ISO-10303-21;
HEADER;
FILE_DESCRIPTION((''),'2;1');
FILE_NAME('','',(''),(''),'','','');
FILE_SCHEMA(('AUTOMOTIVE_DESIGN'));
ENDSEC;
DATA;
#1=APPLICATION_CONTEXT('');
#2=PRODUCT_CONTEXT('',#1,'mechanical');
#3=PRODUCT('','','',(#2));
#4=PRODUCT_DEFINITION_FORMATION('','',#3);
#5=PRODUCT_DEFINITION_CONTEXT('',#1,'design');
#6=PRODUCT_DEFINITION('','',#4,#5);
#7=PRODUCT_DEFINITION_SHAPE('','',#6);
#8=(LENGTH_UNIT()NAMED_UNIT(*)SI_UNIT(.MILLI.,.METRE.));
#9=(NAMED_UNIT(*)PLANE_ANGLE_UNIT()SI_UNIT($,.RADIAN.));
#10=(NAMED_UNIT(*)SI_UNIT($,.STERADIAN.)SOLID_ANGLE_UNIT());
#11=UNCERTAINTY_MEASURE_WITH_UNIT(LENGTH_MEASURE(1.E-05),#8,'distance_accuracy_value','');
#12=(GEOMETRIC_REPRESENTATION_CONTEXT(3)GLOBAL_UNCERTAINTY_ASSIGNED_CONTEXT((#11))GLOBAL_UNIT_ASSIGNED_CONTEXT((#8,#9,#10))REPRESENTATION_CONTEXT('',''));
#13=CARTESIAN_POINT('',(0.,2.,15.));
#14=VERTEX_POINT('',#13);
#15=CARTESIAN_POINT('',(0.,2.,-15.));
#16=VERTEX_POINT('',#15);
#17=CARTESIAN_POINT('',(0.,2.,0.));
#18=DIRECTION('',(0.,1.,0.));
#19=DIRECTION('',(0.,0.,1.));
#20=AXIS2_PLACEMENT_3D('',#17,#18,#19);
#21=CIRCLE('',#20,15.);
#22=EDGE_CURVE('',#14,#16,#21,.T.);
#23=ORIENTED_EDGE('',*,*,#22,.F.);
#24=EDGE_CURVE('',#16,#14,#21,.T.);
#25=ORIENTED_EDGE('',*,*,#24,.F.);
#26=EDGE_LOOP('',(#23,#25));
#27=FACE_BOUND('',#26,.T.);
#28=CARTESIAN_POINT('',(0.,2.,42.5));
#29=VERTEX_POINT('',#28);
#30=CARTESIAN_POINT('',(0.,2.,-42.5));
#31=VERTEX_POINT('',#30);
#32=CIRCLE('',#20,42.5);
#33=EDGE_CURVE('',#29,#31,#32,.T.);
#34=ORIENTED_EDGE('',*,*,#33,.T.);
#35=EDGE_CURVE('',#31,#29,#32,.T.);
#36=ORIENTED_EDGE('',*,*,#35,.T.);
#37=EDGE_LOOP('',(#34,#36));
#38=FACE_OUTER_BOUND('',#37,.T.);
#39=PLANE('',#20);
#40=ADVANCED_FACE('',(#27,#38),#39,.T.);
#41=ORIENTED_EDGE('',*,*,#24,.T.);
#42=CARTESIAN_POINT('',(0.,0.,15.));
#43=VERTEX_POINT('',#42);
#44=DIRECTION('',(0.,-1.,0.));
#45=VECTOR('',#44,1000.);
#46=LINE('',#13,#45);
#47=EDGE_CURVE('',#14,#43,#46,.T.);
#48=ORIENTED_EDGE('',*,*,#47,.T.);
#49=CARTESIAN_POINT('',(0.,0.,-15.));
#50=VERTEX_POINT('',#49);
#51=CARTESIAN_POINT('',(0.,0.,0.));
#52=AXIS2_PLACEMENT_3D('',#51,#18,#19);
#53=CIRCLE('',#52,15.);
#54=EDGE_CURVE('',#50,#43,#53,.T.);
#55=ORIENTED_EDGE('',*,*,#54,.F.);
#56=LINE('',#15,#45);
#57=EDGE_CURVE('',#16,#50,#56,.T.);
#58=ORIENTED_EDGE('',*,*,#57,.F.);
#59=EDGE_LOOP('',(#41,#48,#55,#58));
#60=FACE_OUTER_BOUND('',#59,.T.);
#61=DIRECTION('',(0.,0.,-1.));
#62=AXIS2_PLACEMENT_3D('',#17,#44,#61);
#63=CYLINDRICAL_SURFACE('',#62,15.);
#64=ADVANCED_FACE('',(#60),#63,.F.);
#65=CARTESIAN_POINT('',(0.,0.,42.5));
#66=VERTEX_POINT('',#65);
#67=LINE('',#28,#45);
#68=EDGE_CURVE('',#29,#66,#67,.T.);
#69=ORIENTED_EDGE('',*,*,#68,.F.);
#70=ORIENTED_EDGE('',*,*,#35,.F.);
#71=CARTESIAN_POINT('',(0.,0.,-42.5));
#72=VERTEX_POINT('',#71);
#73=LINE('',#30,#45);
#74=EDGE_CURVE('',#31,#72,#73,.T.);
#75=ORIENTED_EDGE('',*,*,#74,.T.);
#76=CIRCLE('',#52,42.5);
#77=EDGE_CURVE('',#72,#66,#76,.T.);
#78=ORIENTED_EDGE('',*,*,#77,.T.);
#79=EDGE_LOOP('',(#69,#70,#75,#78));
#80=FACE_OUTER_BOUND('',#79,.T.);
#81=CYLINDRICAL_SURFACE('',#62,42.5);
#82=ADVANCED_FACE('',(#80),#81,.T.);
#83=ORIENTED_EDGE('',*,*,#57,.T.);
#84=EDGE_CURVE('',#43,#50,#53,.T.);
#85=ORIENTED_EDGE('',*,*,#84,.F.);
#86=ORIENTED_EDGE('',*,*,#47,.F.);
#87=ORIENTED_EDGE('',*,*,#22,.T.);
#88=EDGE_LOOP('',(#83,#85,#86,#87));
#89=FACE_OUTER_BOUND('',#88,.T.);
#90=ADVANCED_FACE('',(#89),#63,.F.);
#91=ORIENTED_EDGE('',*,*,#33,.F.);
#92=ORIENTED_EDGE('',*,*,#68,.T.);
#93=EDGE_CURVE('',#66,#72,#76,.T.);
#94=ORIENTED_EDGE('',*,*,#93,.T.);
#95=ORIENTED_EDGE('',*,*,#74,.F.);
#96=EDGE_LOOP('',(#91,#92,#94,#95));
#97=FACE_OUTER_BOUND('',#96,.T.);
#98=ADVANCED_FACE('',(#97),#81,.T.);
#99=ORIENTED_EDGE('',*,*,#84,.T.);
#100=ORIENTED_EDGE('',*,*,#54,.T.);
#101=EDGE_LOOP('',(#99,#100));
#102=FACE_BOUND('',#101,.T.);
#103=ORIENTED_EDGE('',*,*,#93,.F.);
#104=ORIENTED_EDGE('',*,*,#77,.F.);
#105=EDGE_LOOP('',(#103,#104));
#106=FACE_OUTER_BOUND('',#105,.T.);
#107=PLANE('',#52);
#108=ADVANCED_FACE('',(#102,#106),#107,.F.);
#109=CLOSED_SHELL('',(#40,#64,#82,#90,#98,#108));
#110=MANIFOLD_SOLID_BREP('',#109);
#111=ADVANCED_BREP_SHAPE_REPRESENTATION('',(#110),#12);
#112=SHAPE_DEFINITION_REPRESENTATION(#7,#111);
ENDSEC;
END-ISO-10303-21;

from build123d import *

# Parameters (mm, degrees)
SKETCH1_R           = 42.5
SKETCH1_R_2         = 15
BOSS_EXTRUDE1_DEPTH = 2


with BuildPart() as part:
    # Sketch1 → Boss-Extrude1 (new body)
    with BuildSketch(Plane(origin=(0, 0, 0), x_dir=(1, 0, 0), z_dir=(0, 1, 0))):
        with Locations(Location((0, 0, 0), (0, 0, 270))):
            Circle(SKETCH1_R)
        with Locations(Location((0, 0, 0), (0, 0, 270))):
            Circle(SKETCH1_R_2, mode=Mode.SUBTRACT)
    extrude(amount=BOSS_EXTRUDE1_DEPTH)


solid = part.part
